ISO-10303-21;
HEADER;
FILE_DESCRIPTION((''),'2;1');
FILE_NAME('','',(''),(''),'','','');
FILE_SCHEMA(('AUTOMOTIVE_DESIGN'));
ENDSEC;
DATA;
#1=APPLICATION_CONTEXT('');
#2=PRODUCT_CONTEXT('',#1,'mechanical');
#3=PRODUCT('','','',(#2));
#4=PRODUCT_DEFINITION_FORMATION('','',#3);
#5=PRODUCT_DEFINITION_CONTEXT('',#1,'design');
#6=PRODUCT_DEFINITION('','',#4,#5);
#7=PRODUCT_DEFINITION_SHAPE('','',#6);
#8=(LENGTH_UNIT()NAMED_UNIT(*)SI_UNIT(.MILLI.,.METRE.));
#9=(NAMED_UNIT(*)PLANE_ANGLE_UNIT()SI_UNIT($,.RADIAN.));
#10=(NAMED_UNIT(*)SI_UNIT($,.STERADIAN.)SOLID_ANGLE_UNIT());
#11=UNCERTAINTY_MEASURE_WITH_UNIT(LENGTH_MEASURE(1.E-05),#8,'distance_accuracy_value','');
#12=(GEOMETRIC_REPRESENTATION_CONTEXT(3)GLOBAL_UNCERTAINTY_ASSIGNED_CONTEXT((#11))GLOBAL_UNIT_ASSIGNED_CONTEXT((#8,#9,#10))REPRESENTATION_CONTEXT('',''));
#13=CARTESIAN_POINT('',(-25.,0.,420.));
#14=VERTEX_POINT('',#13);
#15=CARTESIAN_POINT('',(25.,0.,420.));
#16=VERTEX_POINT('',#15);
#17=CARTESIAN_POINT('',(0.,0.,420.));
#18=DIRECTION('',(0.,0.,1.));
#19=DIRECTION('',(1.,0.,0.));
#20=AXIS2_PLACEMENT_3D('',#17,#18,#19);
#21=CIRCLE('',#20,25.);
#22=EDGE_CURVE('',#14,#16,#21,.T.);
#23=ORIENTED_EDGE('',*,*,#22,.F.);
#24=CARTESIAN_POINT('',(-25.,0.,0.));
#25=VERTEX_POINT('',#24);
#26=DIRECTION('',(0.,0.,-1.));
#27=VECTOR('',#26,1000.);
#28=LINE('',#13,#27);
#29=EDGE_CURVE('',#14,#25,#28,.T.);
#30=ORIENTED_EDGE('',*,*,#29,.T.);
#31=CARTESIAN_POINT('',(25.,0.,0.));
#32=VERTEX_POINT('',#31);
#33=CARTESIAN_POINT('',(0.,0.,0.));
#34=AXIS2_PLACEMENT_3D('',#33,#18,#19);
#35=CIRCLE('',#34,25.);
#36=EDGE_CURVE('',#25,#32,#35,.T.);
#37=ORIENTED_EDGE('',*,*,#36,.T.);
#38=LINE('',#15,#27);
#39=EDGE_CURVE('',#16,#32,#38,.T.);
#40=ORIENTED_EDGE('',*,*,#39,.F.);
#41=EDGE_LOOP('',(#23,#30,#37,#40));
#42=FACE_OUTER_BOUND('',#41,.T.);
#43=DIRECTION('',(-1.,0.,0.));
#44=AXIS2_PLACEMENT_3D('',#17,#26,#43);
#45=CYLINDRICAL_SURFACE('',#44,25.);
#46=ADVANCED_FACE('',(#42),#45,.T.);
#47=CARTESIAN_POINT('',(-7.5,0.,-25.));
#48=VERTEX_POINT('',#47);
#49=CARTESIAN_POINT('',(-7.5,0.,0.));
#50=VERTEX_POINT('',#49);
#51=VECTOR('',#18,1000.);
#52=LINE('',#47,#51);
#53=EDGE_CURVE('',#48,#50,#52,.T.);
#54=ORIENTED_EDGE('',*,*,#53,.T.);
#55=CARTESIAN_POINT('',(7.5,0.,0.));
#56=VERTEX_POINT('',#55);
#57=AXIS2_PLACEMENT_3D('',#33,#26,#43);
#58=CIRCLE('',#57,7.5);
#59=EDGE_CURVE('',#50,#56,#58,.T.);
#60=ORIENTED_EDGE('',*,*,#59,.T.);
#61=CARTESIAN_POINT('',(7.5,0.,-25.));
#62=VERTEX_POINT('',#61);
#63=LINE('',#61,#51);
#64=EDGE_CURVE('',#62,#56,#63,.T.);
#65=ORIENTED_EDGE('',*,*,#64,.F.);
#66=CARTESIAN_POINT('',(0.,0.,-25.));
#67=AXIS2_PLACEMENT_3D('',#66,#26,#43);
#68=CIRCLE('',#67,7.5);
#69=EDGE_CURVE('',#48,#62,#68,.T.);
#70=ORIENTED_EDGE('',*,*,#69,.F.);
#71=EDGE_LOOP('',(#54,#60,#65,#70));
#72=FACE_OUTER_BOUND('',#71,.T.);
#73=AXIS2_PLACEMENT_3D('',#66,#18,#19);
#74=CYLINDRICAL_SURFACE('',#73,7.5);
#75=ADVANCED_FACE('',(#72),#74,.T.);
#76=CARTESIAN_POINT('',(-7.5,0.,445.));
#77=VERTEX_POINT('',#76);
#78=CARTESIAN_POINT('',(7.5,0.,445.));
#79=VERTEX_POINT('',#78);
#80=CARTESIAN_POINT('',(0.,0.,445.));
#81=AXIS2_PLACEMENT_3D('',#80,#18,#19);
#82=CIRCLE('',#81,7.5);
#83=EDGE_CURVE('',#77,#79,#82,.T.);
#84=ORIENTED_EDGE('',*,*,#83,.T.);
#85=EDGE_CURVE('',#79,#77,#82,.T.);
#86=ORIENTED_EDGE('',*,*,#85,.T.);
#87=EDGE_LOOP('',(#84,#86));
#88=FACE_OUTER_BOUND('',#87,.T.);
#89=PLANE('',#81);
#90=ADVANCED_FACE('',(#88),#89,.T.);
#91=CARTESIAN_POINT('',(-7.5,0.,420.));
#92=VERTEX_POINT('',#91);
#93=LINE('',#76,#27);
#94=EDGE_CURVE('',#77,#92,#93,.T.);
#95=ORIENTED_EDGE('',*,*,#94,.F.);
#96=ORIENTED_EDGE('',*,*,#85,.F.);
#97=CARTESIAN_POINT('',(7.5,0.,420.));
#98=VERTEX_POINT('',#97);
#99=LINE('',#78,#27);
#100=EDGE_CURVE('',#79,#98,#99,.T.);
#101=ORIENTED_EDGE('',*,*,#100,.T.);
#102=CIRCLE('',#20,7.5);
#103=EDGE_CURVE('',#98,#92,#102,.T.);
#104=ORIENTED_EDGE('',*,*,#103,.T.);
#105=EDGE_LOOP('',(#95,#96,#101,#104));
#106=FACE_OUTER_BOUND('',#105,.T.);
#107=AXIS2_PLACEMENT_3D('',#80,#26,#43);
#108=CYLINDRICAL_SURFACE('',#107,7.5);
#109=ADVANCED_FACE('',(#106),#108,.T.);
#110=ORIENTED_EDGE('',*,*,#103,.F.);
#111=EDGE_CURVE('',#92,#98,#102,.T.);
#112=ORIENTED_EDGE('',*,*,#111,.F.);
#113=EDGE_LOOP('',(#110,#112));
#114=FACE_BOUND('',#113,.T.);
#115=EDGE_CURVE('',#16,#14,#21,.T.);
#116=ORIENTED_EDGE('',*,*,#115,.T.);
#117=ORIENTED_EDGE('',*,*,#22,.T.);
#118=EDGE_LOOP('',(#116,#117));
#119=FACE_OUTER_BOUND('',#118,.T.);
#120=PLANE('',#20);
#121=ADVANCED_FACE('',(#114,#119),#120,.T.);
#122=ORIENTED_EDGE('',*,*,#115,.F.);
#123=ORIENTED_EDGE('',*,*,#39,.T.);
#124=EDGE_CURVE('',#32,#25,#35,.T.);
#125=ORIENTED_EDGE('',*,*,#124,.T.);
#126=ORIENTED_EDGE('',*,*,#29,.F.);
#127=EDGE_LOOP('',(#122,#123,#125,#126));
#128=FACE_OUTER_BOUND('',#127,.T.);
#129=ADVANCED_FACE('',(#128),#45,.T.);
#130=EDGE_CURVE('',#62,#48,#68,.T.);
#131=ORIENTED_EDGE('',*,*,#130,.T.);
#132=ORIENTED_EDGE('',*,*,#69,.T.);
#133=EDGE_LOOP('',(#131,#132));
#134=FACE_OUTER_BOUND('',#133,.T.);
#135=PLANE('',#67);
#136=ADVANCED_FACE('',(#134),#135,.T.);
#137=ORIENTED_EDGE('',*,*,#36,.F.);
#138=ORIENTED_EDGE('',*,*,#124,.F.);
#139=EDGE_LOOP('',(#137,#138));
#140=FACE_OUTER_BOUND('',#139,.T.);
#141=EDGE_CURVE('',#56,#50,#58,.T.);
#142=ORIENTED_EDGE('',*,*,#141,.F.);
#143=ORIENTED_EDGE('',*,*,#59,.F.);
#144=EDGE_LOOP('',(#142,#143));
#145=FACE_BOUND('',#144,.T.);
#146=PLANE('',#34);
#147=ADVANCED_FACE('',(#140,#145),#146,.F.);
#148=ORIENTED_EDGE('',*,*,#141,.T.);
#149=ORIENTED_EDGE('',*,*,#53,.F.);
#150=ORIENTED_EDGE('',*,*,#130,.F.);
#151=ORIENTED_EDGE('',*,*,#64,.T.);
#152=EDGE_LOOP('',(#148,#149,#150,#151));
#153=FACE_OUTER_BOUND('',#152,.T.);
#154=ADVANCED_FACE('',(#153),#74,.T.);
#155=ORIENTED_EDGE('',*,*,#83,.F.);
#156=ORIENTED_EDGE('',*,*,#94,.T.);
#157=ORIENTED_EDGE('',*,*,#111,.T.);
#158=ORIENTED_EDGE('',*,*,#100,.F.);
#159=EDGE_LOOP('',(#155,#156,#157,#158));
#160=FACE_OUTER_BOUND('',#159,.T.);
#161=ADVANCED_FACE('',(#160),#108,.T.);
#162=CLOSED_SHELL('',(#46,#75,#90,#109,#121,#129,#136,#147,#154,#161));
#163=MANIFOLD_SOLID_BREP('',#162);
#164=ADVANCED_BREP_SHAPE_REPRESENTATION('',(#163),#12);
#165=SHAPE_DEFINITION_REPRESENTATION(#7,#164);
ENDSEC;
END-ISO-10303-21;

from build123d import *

# Parameters (mm, degrees)
SKETCH_1_R      = 25
EXTRUDE_1_DEPTH = 420
SKETCH_2_R      = 7.5
EXTRUDE_2_DEPTH = 25
EXTRUDE_START   = 25
SKETCH_3_R      = 7.5
EXTRUDE_3_DEPTH = 25


with BuildPart() as part:
    # 草图1 → 凸台-拉伸1 (new body)
    with BuildSketch(Plane.XY):
        Circle(SKETCH_1_R)
    extrude(amount=EXTRUDE_1_DEPTH)

    # 草图2 → 凸台-拉伸2 (add)
    with BuildSketch(Plane.XY.offset(420)):
        Circle(SKETCH_2_R)
    extrude(amount=EXTRUDE_2_DEPTH)

    # 草图3 → 凸台-拉伸3 (add)
    with BuildSketch(Plane(origin=(0, 0, 0), x_dir=(-1, 0, 0), z_dir=(0, 0, -1)).offset(EXTRUDE_START)):
        with Locations(Location((0, 0, 0), (0, 0, 180))):
            Circle(SKETCH_3_R)
    extrude(amount=-EXTRUDE_3_DEPTH)


solid = part.part
